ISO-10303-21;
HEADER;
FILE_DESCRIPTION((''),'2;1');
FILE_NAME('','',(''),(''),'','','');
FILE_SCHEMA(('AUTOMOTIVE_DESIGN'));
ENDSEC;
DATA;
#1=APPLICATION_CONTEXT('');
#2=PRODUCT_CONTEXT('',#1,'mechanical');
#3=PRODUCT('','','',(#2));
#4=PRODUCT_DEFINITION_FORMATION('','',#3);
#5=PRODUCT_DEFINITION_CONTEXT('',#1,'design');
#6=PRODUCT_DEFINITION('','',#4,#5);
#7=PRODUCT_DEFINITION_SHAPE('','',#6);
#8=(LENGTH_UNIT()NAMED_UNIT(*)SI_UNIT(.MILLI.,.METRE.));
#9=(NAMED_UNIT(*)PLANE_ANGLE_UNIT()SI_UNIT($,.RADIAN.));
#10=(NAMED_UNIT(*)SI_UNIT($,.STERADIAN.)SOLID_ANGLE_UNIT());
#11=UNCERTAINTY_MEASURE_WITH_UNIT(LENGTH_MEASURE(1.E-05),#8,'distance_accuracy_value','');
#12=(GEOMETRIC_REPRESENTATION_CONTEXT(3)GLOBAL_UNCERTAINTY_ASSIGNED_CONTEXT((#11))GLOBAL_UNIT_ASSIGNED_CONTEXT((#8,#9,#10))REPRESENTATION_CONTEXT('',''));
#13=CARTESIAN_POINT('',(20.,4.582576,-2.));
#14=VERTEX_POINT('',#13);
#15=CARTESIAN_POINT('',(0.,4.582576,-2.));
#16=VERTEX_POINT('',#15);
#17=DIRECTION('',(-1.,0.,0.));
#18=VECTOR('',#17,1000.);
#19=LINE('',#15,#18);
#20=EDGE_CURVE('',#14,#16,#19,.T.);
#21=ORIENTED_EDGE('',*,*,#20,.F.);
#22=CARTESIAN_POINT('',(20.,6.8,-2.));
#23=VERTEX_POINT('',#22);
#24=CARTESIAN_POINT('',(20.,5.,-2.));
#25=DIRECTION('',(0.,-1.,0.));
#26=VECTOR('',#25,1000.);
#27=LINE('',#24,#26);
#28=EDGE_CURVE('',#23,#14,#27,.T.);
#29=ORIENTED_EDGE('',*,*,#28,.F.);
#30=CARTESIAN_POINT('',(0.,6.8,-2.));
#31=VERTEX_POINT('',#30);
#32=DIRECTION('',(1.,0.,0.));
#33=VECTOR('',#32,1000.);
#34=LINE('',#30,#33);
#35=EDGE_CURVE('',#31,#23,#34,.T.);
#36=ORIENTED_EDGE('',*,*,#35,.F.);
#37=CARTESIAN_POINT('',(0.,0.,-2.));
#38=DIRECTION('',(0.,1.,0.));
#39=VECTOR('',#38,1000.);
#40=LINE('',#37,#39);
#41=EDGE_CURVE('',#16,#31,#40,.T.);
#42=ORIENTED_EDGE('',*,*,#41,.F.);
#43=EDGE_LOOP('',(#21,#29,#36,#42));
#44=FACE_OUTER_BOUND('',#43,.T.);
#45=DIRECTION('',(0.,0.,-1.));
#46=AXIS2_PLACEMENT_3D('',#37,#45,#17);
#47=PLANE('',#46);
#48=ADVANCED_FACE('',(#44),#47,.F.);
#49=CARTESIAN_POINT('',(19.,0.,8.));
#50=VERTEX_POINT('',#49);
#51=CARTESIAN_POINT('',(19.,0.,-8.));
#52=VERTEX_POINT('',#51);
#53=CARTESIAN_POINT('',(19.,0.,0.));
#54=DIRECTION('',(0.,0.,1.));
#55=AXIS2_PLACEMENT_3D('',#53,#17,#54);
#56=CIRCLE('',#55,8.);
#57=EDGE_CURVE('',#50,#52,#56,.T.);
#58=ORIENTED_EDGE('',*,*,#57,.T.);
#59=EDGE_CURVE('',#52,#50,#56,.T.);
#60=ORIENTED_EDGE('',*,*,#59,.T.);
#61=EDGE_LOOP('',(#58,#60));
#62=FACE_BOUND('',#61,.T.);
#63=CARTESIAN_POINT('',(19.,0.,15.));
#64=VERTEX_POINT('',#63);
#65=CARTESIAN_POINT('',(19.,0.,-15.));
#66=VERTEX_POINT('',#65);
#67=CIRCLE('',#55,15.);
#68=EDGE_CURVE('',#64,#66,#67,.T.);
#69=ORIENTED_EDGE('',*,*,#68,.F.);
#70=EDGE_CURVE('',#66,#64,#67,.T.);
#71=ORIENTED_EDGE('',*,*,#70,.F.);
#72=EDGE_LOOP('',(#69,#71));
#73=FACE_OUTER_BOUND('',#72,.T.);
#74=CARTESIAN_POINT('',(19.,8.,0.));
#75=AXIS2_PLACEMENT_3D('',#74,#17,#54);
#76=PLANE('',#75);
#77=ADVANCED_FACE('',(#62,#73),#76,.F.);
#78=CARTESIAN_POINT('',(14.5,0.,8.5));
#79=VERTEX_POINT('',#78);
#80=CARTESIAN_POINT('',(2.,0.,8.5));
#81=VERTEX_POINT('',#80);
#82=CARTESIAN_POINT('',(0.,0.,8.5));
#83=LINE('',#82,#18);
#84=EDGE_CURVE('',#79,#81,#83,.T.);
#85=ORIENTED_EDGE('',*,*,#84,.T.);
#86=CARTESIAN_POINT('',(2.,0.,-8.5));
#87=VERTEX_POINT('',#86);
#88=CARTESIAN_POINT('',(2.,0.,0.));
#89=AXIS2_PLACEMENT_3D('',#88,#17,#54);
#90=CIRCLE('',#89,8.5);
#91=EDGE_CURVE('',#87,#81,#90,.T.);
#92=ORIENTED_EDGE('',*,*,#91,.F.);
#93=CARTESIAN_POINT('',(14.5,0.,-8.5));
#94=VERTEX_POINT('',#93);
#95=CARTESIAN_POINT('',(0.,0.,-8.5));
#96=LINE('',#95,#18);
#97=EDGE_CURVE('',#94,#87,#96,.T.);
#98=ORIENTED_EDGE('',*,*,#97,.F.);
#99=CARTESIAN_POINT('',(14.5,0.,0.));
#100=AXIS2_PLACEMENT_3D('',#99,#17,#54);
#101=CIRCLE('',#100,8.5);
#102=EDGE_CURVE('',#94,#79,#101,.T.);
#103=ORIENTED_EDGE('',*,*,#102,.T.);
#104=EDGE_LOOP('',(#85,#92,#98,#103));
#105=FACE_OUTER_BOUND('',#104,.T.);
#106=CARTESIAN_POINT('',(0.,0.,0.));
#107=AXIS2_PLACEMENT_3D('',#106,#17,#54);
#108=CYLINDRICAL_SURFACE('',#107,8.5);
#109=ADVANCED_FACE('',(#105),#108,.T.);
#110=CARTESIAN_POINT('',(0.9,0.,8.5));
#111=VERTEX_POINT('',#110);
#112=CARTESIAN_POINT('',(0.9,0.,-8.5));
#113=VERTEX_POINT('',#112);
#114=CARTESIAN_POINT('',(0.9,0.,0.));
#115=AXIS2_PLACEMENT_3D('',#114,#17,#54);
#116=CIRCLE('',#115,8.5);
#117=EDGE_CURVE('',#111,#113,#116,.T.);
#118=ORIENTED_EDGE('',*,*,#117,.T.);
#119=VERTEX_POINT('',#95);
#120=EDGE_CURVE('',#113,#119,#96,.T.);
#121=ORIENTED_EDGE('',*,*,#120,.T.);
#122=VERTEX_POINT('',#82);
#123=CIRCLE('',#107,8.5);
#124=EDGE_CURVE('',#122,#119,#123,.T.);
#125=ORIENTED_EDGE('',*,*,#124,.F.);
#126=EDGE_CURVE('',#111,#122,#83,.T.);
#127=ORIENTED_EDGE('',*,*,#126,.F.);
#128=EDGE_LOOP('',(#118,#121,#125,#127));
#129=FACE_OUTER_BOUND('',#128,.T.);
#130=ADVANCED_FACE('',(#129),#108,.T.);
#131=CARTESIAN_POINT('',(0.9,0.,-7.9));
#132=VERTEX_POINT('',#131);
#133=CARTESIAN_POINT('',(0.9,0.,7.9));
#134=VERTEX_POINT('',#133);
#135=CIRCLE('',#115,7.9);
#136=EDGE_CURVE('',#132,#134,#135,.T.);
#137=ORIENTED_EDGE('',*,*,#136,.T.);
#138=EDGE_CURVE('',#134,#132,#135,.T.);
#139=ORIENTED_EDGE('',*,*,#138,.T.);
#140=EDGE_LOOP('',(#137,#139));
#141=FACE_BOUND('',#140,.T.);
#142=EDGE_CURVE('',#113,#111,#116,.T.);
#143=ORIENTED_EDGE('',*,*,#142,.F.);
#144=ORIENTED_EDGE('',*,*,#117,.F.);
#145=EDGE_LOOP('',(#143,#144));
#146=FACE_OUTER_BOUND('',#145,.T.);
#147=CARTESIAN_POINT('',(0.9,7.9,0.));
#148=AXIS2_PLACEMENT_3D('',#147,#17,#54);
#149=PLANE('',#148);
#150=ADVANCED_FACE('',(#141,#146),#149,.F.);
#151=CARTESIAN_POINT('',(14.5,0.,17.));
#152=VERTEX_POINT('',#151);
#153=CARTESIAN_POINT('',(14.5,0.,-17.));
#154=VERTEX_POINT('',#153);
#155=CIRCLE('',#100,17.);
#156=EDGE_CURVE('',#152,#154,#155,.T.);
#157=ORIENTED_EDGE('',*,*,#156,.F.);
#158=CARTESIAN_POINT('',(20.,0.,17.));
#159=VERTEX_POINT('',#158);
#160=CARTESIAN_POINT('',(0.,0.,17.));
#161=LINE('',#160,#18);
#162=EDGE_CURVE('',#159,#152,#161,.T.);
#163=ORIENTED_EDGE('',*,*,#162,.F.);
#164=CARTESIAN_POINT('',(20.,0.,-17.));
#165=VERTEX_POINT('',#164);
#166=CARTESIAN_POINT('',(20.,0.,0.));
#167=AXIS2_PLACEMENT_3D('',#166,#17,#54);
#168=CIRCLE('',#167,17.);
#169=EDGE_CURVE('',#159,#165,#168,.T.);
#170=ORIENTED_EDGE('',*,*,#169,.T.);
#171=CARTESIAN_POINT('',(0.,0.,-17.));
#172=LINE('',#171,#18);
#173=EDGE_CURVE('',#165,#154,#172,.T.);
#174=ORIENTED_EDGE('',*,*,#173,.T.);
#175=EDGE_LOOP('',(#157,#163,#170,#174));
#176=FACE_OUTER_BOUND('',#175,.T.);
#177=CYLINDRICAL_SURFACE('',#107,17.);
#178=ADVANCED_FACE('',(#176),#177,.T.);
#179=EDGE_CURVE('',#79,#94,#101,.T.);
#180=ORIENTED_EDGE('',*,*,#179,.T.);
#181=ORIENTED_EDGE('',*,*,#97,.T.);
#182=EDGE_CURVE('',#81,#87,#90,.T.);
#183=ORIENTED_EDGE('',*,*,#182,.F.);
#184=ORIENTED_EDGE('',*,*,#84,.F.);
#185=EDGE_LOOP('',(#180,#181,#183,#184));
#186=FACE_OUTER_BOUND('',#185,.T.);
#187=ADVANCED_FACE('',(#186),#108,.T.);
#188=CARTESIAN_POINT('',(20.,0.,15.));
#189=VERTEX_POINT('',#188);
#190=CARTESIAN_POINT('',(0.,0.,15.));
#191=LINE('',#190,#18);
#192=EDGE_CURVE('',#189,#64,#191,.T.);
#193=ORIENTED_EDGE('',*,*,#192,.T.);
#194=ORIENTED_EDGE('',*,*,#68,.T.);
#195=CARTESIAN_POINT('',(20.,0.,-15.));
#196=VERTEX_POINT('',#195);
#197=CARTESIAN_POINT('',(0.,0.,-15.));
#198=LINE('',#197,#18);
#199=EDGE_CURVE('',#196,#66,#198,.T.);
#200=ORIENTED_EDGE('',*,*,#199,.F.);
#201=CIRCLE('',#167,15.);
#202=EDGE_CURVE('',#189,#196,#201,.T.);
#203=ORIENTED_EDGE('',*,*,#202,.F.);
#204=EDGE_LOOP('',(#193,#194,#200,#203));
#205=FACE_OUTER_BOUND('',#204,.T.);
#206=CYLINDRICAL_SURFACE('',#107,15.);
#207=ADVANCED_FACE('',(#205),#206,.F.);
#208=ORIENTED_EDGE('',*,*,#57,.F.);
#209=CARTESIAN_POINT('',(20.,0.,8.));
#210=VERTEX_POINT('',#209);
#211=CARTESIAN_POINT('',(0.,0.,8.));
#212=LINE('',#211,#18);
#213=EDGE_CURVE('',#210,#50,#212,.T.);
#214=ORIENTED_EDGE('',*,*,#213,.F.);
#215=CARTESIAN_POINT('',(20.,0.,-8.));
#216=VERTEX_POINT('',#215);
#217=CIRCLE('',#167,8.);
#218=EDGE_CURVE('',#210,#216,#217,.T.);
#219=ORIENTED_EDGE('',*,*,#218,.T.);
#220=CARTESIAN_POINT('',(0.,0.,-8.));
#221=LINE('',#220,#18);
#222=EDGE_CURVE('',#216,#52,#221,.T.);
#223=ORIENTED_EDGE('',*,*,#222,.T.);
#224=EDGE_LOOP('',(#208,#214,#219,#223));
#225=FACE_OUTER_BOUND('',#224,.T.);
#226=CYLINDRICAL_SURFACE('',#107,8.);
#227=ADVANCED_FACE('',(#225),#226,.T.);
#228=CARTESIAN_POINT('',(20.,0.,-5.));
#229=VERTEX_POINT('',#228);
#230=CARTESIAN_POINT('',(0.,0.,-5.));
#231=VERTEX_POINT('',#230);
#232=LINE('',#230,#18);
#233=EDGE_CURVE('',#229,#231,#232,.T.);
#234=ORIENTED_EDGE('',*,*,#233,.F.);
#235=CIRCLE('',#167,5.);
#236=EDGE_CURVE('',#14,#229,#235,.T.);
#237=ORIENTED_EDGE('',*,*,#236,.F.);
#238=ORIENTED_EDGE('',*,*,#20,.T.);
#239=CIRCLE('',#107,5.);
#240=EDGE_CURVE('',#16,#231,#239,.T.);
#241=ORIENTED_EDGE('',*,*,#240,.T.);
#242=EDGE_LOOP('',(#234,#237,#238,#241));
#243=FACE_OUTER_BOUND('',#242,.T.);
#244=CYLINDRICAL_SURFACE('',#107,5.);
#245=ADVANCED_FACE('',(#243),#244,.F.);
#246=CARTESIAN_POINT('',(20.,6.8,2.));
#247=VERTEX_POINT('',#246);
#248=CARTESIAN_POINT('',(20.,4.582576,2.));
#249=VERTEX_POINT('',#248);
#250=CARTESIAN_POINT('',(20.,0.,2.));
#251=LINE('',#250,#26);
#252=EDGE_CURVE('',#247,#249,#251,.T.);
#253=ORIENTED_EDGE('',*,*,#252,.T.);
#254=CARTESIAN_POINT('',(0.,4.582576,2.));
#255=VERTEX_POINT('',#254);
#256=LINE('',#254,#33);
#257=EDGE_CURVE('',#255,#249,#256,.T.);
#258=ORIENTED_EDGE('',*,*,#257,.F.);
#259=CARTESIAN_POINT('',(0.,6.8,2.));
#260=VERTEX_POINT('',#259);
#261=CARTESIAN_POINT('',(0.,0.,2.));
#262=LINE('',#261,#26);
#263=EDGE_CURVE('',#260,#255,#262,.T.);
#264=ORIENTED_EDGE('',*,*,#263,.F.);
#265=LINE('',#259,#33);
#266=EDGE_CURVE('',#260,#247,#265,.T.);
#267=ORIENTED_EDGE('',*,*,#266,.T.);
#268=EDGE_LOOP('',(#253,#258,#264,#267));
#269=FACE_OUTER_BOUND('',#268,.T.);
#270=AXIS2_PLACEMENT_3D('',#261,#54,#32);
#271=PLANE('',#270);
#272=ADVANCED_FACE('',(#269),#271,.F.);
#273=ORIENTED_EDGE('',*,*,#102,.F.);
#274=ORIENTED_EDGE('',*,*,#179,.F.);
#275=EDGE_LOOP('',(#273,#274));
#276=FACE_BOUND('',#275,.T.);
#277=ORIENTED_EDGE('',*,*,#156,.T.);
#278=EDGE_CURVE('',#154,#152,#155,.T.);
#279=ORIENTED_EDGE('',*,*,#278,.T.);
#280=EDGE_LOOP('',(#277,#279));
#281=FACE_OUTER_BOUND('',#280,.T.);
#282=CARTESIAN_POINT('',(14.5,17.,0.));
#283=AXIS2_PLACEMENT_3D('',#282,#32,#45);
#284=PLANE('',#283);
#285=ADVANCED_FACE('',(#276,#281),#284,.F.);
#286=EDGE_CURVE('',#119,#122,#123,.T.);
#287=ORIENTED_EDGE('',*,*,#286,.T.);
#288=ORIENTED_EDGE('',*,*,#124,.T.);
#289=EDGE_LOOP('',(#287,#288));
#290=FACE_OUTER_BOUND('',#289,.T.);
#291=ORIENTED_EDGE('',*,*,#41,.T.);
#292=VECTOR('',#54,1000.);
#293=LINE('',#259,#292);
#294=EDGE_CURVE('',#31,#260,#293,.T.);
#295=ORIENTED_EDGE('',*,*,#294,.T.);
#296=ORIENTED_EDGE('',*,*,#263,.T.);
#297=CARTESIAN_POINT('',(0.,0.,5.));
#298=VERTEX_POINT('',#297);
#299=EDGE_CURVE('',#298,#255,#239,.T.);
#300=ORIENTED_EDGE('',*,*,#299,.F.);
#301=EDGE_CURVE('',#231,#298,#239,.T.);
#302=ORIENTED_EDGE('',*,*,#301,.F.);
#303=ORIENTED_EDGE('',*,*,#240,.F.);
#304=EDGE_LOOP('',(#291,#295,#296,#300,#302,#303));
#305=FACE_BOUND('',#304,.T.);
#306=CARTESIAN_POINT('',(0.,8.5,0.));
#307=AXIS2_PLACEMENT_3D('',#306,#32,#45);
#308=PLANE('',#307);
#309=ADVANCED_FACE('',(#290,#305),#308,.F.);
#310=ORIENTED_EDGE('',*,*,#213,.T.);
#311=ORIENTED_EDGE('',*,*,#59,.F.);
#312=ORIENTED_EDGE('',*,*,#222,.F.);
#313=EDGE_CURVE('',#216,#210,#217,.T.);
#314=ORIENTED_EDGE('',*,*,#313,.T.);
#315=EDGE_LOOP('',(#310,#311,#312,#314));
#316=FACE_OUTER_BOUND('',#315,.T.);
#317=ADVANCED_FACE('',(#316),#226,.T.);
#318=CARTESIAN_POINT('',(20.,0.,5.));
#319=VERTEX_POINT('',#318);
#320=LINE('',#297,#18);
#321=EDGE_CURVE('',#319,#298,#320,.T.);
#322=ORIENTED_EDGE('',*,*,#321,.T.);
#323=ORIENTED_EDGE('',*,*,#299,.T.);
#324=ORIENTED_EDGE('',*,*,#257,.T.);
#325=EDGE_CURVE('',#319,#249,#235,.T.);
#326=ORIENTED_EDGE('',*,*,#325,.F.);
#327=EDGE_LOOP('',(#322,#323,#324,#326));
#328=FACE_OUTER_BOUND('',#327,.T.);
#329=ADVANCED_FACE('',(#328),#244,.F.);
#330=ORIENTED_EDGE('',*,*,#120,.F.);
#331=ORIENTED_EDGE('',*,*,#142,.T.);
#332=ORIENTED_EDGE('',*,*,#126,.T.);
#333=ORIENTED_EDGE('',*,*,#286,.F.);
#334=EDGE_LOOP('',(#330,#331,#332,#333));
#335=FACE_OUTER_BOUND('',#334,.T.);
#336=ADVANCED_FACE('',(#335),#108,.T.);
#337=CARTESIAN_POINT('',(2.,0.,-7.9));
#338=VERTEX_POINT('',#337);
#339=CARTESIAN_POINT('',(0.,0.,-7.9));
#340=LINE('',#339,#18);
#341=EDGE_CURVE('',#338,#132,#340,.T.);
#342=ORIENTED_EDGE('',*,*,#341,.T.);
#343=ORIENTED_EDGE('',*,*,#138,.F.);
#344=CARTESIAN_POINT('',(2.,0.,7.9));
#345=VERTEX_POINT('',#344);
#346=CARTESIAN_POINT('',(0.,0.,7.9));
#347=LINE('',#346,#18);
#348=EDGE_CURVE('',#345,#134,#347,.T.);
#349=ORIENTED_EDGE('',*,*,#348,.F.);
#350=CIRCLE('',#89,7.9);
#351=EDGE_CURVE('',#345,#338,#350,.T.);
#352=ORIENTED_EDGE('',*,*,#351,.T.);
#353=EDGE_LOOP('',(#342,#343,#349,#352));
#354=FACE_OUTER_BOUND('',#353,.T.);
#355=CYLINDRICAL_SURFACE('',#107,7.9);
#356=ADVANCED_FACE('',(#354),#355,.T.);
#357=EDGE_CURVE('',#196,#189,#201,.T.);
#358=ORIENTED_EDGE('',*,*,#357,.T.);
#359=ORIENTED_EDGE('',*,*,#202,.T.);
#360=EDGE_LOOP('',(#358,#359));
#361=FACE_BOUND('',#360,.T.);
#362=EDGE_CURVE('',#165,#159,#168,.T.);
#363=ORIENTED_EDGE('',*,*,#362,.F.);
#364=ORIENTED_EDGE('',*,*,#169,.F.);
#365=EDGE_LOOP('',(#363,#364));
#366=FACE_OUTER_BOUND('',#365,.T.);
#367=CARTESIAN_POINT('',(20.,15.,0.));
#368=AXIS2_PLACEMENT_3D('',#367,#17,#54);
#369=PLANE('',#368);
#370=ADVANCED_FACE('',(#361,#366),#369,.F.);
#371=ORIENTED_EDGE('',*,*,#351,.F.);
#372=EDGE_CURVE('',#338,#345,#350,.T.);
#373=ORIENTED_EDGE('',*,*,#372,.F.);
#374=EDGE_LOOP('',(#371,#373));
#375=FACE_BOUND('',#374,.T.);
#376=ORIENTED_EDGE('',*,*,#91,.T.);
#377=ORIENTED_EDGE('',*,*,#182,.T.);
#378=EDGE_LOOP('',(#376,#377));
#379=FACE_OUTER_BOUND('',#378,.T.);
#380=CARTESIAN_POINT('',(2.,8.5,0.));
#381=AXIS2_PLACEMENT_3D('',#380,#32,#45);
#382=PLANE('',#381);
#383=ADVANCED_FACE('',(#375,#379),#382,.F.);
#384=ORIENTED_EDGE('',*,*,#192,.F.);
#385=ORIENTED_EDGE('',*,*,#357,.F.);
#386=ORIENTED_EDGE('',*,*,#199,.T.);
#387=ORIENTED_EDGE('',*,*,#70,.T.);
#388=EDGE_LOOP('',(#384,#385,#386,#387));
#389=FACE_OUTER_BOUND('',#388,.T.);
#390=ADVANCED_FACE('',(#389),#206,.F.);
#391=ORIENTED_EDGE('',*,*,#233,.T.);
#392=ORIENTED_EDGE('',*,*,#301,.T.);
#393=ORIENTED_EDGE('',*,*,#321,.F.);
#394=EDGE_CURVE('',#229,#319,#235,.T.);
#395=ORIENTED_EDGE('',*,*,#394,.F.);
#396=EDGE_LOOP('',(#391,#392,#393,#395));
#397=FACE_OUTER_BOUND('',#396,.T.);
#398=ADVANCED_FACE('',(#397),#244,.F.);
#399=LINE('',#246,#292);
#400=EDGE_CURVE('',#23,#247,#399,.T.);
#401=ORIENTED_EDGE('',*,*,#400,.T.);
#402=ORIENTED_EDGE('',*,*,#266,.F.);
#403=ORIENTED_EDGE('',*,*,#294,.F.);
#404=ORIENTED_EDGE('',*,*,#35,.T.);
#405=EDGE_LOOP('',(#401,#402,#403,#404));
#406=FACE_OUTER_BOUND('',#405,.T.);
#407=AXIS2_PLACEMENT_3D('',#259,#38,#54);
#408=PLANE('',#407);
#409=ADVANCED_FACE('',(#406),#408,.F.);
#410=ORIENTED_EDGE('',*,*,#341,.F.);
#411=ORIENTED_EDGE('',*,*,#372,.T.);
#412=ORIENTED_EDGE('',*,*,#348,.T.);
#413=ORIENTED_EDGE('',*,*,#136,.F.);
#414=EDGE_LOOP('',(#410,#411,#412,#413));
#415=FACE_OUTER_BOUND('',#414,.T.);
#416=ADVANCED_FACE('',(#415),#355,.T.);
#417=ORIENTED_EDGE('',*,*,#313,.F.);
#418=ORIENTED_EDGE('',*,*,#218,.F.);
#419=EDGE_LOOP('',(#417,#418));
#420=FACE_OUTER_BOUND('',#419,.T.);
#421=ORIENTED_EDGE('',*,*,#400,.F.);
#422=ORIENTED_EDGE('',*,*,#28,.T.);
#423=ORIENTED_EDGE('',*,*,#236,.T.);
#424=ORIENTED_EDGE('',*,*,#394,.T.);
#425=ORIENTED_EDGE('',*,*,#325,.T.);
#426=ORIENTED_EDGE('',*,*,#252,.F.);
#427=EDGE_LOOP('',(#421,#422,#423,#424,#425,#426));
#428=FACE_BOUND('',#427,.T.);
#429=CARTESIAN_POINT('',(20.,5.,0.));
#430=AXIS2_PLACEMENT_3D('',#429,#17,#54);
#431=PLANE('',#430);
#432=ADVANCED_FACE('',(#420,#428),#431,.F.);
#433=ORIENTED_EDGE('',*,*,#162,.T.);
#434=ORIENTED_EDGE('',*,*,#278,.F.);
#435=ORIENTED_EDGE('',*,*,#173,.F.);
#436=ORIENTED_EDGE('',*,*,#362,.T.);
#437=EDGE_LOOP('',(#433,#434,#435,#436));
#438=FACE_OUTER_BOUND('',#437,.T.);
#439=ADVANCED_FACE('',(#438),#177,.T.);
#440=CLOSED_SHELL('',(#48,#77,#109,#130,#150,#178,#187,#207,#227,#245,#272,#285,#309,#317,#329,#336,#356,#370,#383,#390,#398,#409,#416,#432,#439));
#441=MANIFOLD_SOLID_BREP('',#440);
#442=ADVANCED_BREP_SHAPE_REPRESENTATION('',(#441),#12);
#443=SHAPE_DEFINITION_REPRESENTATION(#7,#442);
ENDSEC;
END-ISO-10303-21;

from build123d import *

# Parameters (mm, degrees)
SKETCH_2_W          = 4
SKETCH_2_H          = 6.8
CUT_EXTRUDE_1_DEPTH = 32.272991542


with BuildPart() as part:
    # 草图1 → 旋转1 (revolve)
    with BuildSketch(Plane.XY, mode=Mode.PRIVATE) as revolve_1_sk:
        Polygon((0, 5), (20, 5), (20, 8), (19, 8), (19, 15), (20, 15), (20, 17), (14.5, 17), (14.5, 8.5), (2, 8.5), (2, 7.9), (0.9, 7.9), (0.9, 8.5), (0, 8.5), align=None)
    revolve(revolve_1_sk.sketch.rotate(Axis((0, 0, 0), (1, 0, 0)), 90), axis=Axis((0, 0, 0), (1, 0, 0)))

    # 草图2 → 切除-拉伸1 (cut, through all)
    with BuildSketch(Plane(origin=(20, 0, 0), x_dir=(0, 0, -1), z_dir=(1, 0, 0))):
        with Locations((0, 3.4)):
            Rectangle(SKETCH_2_W, SKETCH_2_H)
    extrude(amount=-CUT_EXTRUDE_1_DEPTH, mode=Mode.SUBTRACT)


solid = part.part
